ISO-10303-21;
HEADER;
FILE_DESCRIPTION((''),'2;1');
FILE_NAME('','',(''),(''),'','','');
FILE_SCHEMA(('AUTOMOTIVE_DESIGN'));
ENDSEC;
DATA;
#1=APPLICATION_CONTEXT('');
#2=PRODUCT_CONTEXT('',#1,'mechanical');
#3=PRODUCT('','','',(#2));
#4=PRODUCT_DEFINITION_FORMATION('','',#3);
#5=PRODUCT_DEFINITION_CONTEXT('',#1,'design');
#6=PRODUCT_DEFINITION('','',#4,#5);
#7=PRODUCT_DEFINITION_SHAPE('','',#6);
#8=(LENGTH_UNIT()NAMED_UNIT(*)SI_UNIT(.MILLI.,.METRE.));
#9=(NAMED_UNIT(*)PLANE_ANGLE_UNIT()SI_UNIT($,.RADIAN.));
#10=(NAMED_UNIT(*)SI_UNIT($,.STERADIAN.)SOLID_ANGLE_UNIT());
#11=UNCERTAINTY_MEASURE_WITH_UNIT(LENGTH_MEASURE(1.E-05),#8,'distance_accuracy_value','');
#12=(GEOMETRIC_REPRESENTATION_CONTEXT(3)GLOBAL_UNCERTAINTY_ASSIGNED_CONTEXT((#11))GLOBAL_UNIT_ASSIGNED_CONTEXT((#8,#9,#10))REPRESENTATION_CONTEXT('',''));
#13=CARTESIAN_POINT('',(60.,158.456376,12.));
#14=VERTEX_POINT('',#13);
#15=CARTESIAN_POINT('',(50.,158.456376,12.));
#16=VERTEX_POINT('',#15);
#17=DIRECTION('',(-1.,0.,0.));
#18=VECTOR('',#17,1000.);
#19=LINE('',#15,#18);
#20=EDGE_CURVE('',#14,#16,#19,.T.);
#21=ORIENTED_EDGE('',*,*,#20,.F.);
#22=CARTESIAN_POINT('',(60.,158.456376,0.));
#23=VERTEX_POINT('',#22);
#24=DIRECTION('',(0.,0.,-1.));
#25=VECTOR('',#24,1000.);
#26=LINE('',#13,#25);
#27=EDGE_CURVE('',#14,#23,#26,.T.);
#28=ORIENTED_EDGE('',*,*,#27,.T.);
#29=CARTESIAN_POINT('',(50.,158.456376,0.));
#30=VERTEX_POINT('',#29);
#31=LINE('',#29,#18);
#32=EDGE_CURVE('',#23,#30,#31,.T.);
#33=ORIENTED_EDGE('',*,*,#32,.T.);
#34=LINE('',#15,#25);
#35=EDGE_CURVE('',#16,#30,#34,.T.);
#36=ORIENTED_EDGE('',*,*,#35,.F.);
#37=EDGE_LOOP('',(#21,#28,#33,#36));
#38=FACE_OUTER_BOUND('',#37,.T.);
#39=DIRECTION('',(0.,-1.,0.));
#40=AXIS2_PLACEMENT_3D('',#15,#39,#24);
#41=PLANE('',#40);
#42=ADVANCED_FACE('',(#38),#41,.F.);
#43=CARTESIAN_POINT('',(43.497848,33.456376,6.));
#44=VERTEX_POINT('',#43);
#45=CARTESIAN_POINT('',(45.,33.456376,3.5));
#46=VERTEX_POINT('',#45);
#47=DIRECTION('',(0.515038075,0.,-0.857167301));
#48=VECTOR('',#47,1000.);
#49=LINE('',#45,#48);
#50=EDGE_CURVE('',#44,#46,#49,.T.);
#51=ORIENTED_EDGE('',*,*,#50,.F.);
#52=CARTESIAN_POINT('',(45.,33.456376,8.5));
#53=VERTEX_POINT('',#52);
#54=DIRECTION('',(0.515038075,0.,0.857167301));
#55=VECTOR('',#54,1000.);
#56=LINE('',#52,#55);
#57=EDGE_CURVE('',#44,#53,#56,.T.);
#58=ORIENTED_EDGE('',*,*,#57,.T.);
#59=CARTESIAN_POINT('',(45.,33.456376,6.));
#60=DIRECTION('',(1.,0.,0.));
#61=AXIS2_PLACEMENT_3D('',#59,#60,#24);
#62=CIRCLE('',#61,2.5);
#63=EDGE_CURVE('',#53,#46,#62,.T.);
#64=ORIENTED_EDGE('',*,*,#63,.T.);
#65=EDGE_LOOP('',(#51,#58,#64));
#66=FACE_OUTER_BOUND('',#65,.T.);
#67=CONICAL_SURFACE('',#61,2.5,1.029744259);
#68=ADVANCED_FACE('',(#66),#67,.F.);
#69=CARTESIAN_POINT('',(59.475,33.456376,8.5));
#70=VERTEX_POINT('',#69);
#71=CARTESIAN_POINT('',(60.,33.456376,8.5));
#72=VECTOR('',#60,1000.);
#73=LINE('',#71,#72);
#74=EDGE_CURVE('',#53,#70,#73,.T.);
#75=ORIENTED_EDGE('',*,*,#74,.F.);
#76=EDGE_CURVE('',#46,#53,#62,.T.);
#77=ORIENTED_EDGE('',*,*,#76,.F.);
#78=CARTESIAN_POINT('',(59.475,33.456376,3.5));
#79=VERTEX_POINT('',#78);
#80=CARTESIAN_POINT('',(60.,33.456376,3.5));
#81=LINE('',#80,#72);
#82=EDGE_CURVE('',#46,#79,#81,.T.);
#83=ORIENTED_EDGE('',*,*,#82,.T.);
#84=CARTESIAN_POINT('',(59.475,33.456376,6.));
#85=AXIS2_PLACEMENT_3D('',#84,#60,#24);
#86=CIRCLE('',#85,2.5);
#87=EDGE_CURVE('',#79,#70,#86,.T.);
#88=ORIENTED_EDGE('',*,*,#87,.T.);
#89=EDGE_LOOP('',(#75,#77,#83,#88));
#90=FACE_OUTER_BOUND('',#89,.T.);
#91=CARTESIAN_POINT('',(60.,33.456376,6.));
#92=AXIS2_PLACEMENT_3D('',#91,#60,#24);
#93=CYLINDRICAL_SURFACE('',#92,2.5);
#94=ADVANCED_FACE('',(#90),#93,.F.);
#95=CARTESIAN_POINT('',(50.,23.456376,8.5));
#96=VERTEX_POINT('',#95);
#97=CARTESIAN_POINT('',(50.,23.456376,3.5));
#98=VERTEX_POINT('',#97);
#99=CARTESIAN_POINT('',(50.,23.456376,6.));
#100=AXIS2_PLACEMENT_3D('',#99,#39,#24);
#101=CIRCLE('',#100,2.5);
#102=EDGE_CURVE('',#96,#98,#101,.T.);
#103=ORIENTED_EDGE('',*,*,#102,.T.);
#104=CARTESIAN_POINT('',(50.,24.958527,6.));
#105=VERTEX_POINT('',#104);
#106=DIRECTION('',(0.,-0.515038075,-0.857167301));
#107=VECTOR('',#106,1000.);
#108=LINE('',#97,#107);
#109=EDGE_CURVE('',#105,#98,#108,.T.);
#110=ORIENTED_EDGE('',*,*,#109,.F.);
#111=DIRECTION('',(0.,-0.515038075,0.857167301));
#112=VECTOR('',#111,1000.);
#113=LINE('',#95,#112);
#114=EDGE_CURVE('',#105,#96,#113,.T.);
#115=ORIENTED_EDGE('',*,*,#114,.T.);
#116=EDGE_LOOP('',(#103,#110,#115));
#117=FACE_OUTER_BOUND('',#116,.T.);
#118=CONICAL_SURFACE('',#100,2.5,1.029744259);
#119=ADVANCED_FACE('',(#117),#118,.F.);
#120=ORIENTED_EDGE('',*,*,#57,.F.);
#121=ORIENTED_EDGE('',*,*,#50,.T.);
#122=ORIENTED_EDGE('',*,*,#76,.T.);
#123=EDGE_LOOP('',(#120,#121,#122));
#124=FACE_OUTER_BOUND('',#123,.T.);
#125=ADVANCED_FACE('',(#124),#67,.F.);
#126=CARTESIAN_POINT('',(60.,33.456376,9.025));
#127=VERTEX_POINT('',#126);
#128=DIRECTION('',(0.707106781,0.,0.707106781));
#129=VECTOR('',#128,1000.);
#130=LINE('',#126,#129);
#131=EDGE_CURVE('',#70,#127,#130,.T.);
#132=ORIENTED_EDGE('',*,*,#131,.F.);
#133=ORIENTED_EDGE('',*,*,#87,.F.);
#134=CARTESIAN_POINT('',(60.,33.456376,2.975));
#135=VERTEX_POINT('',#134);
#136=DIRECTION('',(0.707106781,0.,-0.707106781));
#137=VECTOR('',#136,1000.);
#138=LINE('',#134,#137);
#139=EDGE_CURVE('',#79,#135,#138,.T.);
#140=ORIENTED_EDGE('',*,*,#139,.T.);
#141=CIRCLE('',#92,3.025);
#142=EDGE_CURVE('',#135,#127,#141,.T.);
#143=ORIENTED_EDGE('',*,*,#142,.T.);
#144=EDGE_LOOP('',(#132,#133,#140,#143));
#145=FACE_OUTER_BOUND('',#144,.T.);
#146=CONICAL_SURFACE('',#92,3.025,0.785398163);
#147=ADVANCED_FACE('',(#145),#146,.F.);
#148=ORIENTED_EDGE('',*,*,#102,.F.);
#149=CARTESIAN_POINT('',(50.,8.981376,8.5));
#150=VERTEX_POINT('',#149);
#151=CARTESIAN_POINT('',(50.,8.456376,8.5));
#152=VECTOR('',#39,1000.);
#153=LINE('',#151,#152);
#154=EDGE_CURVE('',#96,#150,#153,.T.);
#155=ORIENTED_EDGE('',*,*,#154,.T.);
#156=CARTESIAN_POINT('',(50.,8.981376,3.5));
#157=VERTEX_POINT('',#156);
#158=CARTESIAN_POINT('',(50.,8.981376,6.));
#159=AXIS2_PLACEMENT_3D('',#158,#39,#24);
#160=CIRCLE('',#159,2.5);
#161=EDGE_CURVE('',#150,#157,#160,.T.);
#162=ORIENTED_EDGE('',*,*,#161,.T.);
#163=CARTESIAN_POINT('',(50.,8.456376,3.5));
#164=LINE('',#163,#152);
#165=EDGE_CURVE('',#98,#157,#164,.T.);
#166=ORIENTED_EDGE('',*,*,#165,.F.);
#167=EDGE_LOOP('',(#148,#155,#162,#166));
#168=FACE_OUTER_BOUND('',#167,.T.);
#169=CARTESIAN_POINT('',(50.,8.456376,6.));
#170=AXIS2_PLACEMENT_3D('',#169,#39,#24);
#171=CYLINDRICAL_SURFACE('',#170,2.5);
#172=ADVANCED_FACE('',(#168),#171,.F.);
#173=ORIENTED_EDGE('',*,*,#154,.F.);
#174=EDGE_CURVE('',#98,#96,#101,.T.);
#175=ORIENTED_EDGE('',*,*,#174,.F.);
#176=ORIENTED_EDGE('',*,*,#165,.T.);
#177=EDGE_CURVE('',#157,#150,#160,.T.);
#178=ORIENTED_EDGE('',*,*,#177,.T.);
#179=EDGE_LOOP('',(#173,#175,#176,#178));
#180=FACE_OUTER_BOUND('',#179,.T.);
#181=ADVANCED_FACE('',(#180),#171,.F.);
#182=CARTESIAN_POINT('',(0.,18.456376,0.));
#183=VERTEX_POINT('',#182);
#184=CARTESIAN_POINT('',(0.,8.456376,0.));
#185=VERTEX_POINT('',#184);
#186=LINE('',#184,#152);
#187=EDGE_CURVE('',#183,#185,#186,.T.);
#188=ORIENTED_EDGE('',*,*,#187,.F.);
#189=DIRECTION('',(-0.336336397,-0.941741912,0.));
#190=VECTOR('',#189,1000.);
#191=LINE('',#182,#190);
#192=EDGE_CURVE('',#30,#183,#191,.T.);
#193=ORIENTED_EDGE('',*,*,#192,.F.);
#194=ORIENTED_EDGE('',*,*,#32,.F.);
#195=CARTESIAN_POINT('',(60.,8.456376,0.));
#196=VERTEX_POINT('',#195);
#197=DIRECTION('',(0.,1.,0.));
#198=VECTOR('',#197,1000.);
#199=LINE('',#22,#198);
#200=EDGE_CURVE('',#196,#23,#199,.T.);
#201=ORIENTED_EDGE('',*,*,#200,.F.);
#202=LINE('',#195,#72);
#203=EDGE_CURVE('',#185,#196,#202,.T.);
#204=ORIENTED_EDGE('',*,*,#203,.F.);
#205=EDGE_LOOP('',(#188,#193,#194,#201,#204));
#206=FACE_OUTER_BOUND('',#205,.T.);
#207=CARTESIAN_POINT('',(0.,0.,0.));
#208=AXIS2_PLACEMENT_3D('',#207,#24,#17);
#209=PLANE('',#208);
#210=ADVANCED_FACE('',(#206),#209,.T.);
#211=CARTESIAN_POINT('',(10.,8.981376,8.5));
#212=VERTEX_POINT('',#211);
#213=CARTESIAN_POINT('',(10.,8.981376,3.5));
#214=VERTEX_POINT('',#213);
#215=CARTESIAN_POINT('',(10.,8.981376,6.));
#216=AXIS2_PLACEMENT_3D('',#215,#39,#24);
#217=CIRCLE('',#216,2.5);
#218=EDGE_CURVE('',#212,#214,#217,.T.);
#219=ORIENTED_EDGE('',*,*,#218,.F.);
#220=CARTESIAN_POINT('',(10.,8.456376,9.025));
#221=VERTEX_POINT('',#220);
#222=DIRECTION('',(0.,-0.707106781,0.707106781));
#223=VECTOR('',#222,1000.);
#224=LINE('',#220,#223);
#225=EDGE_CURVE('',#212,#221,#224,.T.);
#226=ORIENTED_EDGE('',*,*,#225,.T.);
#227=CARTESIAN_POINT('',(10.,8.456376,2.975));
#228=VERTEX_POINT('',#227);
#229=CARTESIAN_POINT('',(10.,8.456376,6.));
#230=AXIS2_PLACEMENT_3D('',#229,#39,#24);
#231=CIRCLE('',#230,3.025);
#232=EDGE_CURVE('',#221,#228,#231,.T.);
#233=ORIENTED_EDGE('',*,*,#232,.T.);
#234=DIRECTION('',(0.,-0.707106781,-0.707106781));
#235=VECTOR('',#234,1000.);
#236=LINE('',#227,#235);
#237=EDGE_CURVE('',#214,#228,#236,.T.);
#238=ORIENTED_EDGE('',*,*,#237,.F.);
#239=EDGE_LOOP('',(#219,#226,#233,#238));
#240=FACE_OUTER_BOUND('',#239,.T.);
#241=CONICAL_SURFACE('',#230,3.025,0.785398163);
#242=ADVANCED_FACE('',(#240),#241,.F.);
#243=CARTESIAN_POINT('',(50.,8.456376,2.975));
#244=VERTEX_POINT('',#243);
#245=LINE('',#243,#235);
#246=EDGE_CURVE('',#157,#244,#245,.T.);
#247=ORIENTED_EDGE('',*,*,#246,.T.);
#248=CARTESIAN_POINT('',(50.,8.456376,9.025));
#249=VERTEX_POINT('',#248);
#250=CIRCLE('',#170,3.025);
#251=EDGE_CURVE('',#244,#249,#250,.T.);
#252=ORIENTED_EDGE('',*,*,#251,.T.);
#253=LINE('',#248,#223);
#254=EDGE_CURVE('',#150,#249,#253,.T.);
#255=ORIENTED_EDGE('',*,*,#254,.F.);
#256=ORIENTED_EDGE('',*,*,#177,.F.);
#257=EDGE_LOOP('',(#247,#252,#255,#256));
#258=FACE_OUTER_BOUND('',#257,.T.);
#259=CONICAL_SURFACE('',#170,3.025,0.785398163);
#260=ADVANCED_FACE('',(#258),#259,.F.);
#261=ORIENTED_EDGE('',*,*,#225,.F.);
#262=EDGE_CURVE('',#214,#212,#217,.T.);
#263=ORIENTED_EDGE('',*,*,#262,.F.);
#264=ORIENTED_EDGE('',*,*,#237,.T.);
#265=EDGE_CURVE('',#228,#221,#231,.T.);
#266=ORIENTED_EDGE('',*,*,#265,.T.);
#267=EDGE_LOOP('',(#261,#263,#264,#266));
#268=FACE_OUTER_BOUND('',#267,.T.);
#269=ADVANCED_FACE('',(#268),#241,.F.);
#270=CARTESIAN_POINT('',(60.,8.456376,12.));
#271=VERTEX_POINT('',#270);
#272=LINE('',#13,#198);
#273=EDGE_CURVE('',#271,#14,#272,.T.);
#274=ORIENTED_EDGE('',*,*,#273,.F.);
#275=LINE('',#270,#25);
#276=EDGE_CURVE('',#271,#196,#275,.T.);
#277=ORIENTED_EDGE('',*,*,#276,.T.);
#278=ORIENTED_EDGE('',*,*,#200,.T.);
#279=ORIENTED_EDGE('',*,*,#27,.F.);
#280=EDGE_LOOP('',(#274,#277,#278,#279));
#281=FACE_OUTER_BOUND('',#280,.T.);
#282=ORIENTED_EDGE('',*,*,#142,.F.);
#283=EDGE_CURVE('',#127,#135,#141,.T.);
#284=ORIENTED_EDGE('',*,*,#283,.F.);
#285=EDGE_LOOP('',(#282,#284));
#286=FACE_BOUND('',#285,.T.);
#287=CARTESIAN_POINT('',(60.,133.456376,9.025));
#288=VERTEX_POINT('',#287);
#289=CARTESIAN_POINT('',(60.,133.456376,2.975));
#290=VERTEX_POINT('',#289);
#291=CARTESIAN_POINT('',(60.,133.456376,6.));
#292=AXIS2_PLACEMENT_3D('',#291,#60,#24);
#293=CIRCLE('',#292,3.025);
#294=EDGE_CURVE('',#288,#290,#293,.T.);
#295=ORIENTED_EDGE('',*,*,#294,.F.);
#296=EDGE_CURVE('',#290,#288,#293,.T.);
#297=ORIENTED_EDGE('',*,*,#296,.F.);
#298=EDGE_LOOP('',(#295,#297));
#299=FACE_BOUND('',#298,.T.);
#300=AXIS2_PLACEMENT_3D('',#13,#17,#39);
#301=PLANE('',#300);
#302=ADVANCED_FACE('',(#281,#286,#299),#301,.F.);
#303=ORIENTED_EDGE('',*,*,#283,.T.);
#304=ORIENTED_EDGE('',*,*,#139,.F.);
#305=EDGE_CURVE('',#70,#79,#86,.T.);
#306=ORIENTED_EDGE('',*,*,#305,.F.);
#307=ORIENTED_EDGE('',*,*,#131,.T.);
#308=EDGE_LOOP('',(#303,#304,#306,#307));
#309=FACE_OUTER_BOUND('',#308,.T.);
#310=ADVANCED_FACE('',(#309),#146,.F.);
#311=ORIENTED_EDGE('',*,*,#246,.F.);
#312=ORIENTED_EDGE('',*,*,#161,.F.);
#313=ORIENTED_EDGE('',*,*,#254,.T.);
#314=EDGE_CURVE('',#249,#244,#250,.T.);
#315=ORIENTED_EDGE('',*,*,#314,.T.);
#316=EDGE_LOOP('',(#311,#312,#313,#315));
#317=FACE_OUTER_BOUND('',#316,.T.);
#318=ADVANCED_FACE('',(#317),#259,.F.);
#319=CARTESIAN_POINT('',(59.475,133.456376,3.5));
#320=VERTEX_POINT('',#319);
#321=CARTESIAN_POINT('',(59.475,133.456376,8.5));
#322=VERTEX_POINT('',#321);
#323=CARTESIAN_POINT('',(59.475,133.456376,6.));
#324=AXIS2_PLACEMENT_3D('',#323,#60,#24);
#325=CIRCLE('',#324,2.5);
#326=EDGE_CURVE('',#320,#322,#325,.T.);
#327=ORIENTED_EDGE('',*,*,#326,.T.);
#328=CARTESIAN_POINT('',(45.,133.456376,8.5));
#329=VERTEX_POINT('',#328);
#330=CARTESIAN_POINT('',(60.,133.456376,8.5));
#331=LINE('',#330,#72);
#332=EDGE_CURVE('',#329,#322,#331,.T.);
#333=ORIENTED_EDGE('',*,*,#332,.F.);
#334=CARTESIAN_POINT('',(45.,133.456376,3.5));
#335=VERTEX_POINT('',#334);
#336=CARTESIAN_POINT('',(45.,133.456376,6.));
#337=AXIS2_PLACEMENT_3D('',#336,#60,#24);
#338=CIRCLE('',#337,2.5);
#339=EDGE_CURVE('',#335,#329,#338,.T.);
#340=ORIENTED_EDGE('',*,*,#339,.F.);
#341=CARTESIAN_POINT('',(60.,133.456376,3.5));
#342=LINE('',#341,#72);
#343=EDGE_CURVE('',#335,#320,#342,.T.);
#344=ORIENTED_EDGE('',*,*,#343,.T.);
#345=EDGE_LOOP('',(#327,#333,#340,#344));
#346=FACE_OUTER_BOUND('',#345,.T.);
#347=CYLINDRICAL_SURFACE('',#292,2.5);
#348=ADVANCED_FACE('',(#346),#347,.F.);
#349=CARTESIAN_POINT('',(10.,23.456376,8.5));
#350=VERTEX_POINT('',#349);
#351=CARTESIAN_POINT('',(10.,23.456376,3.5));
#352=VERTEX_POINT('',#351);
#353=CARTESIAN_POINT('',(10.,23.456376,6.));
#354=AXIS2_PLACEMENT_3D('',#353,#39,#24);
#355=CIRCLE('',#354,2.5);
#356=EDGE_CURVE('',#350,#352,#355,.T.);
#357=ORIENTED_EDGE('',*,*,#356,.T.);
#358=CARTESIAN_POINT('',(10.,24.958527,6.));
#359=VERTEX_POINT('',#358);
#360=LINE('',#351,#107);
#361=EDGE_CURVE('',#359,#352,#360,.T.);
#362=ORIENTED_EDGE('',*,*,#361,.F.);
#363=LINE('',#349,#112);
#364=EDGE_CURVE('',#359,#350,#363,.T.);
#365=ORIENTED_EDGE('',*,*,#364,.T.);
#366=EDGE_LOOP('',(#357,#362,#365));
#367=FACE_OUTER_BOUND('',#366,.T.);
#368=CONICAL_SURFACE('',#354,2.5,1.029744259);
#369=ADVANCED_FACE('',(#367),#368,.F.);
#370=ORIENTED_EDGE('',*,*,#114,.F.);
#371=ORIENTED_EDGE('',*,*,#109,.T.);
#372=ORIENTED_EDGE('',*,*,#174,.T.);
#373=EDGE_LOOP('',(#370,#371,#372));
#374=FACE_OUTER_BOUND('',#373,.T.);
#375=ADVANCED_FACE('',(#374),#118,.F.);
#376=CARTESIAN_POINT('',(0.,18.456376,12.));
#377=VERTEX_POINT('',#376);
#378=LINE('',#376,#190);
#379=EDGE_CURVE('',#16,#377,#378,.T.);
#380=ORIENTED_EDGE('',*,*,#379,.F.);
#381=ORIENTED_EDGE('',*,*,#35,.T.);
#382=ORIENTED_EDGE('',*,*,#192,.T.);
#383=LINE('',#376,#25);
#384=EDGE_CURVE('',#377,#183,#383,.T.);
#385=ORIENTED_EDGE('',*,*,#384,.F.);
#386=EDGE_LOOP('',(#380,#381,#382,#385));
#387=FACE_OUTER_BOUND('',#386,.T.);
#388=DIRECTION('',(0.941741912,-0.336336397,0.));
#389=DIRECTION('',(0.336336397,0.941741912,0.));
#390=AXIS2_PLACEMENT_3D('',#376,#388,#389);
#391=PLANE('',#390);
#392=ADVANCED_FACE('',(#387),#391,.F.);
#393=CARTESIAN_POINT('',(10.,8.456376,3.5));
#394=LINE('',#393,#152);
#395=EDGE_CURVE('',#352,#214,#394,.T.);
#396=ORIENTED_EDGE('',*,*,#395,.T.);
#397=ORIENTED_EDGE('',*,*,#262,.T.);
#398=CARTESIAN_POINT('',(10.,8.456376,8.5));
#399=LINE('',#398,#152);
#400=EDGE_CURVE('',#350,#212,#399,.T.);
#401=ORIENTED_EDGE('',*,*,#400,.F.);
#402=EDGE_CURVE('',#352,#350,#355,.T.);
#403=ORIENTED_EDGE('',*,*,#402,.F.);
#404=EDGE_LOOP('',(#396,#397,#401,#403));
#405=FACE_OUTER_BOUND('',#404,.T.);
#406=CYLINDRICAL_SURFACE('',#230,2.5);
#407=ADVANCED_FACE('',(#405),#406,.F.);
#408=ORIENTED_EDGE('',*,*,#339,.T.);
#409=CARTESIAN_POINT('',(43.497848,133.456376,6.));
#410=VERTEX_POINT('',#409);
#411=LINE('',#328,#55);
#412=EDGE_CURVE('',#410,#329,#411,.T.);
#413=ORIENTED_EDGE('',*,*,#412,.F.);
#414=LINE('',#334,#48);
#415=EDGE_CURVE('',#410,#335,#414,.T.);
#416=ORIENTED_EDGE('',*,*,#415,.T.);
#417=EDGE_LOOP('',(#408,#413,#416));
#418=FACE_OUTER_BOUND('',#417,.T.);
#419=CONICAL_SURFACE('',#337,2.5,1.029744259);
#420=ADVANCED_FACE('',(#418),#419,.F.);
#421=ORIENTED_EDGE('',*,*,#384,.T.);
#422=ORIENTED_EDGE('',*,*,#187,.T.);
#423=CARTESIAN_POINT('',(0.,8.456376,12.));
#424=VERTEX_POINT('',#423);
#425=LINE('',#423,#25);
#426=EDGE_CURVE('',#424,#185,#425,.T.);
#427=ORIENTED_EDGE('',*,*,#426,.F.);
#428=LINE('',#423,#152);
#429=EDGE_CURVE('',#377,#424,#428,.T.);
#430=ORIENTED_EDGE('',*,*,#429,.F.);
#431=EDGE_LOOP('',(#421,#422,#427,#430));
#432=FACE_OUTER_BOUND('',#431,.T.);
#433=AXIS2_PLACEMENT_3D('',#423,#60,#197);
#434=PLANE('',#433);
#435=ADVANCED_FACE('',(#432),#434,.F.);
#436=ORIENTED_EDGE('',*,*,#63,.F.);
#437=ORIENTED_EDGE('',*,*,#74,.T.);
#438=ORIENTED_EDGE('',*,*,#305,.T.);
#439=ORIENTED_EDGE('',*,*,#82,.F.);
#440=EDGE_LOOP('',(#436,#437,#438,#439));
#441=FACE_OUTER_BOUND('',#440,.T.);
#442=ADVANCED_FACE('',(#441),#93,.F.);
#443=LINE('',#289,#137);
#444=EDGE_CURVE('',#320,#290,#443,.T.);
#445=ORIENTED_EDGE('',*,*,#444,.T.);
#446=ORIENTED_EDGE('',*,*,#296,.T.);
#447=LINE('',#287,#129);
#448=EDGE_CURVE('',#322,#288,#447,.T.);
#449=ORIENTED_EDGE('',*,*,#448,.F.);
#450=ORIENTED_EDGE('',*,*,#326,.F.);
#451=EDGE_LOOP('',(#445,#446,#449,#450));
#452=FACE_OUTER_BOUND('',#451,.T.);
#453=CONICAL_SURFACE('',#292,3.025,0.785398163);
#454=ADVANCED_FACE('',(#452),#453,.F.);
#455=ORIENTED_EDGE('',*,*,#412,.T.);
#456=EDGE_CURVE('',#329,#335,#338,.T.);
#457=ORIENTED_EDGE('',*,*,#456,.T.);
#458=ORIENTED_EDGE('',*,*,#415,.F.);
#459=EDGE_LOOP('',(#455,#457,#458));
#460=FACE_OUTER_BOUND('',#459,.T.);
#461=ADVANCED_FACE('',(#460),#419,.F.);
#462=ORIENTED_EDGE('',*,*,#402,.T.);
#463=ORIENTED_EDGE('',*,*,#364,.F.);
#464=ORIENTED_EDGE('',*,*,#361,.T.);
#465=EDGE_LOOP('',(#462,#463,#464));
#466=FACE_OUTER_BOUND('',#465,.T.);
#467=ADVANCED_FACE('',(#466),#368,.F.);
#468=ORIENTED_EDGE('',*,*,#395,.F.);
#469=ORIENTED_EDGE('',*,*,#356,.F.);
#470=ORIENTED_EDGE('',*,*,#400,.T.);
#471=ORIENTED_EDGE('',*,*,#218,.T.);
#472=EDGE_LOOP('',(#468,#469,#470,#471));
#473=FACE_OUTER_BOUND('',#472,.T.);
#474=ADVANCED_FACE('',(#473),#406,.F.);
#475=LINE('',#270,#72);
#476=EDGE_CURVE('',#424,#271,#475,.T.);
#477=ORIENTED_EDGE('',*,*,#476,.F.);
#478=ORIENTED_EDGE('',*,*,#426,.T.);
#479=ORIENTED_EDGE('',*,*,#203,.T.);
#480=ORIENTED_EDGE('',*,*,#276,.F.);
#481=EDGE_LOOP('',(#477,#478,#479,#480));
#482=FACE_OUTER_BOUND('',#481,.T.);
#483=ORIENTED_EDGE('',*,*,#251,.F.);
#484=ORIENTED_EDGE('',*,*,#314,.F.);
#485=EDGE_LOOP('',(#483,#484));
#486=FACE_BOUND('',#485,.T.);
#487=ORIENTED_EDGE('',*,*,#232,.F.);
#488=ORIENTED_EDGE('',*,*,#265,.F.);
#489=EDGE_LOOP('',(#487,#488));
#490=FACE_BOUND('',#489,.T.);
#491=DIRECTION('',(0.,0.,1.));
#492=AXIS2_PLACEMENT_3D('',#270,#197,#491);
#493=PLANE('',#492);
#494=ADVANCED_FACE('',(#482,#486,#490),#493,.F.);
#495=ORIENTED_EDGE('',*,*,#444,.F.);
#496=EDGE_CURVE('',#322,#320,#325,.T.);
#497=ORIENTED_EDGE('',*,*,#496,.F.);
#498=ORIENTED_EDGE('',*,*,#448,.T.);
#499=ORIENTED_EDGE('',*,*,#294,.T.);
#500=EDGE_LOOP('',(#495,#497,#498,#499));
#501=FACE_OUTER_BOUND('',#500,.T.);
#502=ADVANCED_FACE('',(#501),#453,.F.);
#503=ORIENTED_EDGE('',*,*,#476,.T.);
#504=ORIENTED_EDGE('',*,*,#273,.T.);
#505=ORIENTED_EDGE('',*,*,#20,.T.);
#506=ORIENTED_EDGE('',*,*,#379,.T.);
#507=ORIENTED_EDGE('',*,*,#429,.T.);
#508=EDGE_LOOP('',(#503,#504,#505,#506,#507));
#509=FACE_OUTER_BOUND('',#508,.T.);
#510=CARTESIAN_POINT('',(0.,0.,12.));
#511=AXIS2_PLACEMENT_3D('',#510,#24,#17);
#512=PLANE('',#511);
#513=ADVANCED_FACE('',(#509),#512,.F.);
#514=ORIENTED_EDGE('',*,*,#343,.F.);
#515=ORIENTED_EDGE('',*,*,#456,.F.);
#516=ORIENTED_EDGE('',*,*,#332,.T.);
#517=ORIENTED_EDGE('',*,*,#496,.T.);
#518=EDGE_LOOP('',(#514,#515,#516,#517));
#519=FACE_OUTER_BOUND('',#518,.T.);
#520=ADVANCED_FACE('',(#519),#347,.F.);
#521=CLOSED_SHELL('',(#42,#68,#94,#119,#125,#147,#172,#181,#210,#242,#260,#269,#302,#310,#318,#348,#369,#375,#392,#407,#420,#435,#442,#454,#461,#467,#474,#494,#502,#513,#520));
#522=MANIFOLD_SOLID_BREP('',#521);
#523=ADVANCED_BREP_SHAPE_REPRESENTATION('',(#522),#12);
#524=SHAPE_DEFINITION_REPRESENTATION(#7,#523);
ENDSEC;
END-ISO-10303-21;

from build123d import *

# Parameters (mm, degrees)
EXTRUDE_1_DEPTH              = 12
HOLE_WIZARD_M6_1_D           = 5
HOLE_WIZARD_M6_1_DEPTH       = 15
HOLE_WIZARD_M6_1_CSINK_D     = 6.05
HOLE_WIZARD_M6_1_CSINK_ANGLE = 90
HOLE_WIZARD_M6_1_TIP         = 1.502151548
HOLE_WIZARD_M6_2_D           = 5
HOLE_WIZARD_M6_2_DEPTH       = 15
HOLE_WIZARD_M6_2_CSINK_D     = 6.05
HOLE_WIZARD_M6_2_CSINK_ANGLE = 90
HOLE_WIZARD_M6_2_TIP         = 1.502151548


with BuildPart() as part:
    # 草图1 → 凸台-拉伸1 (new body)
    with BuildSketch(Plane.XY):
        Polygon((0, 8.456375839), (0, 18.456375839), (50, 158.456375839), (60, 158.456375839), (60, 8.456375839), align=None)
    extrude(amount=EXTRUDE_1_DEPTH)

    # M6 螺纹孔1
    with Locations(Plane(origin=(0, 8.456375839, 0), x_dir=(-1, 0, 0), z_dir=(0, -1, 0))):
        with Locations((-50, -6), (-10, -6)):
            CounterSinkHole(HOLE_WIZARD_M6_1_D / 2, HOLE_WIZARD_M6_1_CSINK_D / 2, depth=HOLE_WIZARD_M6_1_DEPTH, counter_sink_angle=HOLE_WIZARD_M6_1_CSINK_ANGLE)
            with Locations((0, 0, -(HOLE_WIZARD_M6_1_DEPTH + HOLE_WIZARD_M6_1_TIP / 2))):  # 118° drill point
                Cone(0, HOLE_WIZARD_M6_1_D / 2, HOLE_WIZARD_M6_1_TIP, mode=Mode.SUBTRACT)

    # M6 螺纹孔2
    with Locations(Plane(origin=(60, 0, 0), x_dir=(0, 0, -1), z_dir=(1, 0, 0))):
        with Locations((-6, 33.456375839), (-6, 133.456375839)):
            CounterSinkHole(HOLE_WIZARD_M6_2_D / 2, HOLE_WIZARD_M6_2_CSINK_D / 2, depth=HOLE_WIZARD_M6_2_DEPTH, counter_sink_angle=HOLE_WIZARD_M6_2_CSINK_ANGLE)
            with Locations((0, 0, -(HOLE_WIZARD_M6_2_DEPTH + HOLE_WIZARD_M6_2_TIP / 2))):  # 118° drill point
                Cone(0, HOLE_WIZARD_M6_2_D / 2, HOLE_WIZARD_M6_2_TIP, mode=Mode.SUBTRACT)


solid = part.part
